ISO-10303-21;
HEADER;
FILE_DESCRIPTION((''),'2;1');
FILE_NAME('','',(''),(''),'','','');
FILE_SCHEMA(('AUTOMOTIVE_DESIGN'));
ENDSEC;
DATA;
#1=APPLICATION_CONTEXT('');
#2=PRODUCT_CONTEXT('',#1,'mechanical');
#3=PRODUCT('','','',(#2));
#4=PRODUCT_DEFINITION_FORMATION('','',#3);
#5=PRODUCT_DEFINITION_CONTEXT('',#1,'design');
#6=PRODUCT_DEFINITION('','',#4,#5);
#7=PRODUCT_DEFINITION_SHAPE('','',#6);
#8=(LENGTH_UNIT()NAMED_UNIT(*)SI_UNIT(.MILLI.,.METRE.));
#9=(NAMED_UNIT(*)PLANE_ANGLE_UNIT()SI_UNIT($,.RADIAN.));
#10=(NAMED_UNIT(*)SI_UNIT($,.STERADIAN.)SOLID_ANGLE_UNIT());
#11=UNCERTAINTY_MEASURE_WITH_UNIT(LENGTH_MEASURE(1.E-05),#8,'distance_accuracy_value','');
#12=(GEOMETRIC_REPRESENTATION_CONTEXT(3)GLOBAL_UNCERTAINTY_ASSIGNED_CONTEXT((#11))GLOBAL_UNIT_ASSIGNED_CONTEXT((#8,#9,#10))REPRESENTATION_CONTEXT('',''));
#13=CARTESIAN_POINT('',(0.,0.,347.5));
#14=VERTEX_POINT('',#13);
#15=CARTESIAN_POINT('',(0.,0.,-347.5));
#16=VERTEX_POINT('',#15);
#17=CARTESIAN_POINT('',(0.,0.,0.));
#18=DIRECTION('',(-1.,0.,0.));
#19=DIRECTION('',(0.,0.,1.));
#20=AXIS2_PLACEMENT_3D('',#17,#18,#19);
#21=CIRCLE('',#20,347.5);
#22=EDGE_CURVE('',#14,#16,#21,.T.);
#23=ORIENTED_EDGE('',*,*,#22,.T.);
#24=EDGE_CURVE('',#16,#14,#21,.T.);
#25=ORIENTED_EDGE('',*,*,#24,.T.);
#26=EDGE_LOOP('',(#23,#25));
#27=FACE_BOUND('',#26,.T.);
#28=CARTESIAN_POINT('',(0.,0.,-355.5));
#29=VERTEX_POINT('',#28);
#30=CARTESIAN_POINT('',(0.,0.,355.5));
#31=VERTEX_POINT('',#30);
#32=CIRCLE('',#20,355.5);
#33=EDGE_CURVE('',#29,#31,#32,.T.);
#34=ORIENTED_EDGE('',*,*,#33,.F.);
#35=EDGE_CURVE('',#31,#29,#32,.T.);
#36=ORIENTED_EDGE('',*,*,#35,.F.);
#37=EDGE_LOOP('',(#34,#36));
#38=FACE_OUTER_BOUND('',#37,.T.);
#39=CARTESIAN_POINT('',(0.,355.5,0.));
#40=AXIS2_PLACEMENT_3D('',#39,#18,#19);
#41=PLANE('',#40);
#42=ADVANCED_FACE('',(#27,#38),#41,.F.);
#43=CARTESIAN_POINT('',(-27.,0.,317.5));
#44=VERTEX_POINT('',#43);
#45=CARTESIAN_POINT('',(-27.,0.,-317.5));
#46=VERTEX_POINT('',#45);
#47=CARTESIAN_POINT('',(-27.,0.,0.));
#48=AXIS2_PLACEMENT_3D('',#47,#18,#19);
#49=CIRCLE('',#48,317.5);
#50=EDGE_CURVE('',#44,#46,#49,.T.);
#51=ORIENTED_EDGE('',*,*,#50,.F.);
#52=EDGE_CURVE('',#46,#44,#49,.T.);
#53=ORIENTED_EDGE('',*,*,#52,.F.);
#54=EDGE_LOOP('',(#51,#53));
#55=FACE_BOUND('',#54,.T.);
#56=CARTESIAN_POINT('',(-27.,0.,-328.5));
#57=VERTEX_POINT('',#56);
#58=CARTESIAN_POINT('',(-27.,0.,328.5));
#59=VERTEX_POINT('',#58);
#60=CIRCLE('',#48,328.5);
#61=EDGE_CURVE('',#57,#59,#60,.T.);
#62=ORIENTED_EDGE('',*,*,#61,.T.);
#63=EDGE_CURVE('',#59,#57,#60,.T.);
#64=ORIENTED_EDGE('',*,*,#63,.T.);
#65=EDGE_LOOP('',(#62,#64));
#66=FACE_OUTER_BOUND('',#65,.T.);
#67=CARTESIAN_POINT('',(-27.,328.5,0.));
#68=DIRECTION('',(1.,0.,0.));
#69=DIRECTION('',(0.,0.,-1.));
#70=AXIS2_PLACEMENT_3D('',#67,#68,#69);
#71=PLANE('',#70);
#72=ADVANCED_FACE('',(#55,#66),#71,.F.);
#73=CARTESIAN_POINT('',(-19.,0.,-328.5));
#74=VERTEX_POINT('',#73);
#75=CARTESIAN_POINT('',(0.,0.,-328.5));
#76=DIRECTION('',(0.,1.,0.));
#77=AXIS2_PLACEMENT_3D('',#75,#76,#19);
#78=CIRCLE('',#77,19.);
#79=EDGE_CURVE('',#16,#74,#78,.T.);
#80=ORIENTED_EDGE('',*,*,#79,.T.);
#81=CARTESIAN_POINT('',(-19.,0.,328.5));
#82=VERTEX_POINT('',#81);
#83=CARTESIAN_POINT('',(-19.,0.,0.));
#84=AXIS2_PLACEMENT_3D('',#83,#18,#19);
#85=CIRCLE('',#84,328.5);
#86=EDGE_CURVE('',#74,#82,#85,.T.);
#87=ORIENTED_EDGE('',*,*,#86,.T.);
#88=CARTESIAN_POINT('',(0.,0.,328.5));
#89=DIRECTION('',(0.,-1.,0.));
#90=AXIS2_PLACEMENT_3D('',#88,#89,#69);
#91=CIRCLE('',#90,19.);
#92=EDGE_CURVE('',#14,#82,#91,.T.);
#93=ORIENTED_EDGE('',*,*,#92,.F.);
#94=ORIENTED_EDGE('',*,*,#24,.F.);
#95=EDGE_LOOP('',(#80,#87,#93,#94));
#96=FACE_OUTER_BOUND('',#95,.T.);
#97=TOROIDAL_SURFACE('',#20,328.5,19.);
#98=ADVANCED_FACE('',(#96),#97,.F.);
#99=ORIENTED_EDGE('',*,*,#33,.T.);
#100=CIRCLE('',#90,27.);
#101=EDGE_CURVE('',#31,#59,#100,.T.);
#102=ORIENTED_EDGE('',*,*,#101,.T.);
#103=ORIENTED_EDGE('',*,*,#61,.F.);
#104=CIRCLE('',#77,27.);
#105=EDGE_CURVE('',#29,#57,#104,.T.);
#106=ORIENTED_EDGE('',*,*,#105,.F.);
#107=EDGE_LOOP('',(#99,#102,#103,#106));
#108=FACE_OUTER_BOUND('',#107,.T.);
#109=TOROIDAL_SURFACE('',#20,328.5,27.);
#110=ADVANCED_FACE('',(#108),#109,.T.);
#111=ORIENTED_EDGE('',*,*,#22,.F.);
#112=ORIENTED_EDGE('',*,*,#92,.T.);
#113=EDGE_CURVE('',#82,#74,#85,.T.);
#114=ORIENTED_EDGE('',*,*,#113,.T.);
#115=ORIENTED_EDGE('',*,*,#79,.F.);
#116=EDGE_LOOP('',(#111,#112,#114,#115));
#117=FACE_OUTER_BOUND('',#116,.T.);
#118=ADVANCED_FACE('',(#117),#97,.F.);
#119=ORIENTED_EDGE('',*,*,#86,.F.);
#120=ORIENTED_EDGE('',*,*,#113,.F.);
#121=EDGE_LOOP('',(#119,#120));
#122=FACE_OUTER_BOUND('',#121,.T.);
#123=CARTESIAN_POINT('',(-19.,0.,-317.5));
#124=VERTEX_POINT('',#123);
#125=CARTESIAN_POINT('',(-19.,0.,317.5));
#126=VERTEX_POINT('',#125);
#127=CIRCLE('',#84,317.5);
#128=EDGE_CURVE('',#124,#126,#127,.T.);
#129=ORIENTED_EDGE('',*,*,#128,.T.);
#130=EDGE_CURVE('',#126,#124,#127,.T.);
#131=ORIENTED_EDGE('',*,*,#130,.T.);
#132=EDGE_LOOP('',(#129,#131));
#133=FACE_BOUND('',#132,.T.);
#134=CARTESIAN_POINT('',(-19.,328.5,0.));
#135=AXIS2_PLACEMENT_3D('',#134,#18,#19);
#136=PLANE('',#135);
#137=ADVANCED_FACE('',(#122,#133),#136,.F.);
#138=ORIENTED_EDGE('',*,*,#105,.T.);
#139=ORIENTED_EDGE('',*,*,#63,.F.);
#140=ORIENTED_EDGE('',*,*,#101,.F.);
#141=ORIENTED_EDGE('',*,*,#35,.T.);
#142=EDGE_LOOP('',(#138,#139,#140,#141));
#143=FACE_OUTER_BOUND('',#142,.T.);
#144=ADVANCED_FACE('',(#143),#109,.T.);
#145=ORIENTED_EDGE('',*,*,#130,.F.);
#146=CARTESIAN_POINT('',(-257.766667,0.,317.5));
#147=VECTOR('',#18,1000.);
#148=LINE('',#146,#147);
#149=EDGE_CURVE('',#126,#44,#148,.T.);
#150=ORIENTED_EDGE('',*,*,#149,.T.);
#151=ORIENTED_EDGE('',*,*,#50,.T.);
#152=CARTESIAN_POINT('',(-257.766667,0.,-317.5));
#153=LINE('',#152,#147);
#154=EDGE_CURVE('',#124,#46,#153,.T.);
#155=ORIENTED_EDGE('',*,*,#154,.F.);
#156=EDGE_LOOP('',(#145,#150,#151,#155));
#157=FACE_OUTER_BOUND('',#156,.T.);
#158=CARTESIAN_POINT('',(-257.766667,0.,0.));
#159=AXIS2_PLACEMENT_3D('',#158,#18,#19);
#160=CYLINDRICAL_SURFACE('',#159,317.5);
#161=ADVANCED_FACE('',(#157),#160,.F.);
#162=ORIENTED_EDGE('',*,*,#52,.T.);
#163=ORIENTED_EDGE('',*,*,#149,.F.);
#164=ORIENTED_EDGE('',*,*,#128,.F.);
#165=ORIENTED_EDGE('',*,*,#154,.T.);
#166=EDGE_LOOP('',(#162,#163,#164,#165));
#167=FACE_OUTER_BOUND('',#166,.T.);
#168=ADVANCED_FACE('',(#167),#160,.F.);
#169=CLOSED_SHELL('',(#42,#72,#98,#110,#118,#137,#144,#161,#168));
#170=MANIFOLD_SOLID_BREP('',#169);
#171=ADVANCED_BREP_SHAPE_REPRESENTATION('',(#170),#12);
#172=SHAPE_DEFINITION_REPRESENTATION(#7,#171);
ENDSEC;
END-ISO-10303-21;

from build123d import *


with BuildPart() as part:
    # 草图1 → 旋转1 (revolve)
    with BuildSketch(Plane.XY, mode=Mode.PRIVATE) as revolve_1_sk:
        with BuildLine():
            Line((-27, 328.5), (-27, 317.5))
            Line((-27, 317.5), (-19, 317.5))
            Line((-19, 317.5), (-19, 328.5))
            ThreePointArc((-19, 328.5), (-13.435028843, 341.935028843), (0, 347.5))
            Line((0, 347.5), (0, 355.5))
            ThreePointArc((0, 355.5), (-19.091883092, 347.591883092), (-27, 328.5))
        make_face()
    revolve(revolve_1_sk.sketch.rotate(Axis((-257.766666667, 0, 0), (1, 0, 0)), 90), axis=Axis((-257.766666667, 0, 0), (1, 0, 0)))


solid = part.part
